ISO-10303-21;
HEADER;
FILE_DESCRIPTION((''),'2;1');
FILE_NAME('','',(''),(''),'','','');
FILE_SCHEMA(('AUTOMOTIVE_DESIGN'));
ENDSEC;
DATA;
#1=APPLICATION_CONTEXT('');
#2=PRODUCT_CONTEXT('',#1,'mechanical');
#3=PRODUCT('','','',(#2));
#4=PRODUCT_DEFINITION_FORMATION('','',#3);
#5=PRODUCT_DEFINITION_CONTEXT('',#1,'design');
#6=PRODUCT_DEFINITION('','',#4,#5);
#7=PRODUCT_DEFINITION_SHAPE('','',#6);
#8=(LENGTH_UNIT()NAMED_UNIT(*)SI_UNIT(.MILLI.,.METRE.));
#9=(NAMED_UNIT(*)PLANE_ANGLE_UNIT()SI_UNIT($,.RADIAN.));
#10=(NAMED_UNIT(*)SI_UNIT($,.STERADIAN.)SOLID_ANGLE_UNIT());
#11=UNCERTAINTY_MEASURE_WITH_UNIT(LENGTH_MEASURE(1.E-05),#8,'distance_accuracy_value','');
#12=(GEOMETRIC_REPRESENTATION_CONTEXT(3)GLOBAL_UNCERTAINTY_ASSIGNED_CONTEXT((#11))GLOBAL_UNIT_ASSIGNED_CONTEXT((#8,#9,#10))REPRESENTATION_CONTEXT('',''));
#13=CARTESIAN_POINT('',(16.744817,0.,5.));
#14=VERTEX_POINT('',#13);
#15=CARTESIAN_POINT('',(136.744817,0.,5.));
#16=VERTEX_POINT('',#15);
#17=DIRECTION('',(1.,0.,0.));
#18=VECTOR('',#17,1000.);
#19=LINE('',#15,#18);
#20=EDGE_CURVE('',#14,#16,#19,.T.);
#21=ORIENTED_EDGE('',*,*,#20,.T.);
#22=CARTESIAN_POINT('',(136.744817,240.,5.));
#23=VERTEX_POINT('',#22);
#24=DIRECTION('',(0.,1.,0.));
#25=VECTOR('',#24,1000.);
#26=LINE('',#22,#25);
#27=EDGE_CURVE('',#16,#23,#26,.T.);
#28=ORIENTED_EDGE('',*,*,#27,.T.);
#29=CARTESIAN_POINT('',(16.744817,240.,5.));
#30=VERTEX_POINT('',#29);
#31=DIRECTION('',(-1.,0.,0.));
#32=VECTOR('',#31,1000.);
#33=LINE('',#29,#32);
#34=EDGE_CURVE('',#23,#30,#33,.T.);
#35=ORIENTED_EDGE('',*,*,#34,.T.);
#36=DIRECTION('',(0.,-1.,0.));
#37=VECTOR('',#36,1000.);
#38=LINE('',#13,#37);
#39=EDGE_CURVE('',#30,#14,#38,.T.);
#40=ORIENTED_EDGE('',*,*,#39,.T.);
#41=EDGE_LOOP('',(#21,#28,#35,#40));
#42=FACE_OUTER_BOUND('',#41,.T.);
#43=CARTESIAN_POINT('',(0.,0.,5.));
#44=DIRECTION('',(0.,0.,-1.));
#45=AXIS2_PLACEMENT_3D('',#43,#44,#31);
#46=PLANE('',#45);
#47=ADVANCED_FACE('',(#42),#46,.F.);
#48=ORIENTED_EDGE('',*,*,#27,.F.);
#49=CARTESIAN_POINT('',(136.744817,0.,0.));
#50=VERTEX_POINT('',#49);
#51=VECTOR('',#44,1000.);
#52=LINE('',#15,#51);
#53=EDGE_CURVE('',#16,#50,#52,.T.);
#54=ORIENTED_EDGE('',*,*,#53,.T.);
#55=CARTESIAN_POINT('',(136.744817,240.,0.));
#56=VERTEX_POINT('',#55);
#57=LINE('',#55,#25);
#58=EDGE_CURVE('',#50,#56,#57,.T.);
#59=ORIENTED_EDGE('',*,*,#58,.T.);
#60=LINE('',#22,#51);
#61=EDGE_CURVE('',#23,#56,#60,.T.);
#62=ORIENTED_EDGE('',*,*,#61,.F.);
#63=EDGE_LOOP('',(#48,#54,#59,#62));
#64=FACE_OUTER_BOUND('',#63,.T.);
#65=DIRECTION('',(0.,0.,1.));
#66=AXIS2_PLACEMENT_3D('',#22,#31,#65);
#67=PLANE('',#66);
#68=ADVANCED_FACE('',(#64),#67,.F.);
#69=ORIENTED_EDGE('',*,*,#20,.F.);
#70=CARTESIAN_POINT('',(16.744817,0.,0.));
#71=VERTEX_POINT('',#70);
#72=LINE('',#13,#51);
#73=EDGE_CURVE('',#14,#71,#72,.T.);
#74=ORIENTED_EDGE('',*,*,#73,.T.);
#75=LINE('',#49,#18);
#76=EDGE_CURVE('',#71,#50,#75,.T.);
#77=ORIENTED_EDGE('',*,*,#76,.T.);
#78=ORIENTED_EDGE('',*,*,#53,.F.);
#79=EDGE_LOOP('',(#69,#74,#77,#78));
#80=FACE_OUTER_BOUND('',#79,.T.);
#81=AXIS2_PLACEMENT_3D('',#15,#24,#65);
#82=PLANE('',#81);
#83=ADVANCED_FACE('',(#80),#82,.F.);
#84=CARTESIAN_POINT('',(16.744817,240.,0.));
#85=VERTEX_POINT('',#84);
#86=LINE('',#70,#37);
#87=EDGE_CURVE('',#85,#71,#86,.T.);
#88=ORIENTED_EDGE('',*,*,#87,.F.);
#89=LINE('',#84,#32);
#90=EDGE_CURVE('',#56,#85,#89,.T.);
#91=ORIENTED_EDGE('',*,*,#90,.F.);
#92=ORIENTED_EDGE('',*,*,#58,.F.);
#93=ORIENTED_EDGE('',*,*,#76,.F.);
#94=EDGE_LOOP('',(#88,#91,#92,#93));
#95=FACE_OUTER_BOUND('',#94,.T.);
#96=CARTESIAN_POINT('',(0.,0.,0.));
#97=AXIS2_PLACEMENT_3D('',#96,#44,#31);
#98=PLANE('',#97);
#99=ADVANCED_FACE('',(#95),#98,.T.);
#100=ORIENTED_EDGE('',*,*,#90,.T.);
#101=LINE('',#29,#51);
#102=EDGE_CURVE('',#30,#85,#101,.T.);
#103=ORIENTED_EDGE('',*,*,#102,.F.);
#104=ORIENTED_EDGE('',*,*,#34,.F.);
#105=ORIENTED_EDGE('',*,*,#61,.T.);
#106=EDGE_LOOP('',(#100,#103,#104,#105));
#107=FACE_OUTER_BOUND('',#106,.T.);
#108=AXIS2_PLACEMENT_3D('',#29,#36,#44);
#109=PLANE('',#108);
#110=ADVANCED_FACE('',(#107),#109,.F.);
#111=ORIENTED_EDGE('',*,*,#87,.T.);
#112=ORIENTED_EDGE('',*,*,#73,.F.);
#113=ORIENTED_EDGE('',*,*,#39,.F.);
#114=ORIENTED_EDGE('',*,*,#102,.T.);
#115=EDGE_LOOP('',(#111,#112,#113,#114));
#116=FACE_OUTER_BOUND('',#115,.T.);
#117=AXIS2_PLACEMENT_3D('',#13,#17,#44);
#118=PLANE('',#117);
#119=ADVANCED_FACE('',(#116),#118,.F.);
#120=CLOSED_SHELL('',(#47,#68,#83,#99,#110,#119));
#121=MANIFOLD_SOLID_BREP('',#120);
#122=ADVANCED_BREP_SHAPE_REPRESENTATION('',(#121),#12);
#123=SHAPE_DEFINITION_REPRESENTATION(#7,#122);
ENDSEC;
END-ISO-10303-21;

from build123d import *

# Parameters (mm, degrees)
SKETCH_1_W      = 120
SKETCH_1_H      = 240
EXTRUDE_1_DEPTH = 5


with BuildPart() as part:
    # 草图1 → 凸台-拉伸1 (new body)
    with BuildSketch(Plane.XY):
        with Locations((76.744816749, 120)):
            Rectangle(SKETCH_1_W, SKETCH_1_H)
    extrude(amount=EXTRUDE_1_DEPTH)


solid = part.part
